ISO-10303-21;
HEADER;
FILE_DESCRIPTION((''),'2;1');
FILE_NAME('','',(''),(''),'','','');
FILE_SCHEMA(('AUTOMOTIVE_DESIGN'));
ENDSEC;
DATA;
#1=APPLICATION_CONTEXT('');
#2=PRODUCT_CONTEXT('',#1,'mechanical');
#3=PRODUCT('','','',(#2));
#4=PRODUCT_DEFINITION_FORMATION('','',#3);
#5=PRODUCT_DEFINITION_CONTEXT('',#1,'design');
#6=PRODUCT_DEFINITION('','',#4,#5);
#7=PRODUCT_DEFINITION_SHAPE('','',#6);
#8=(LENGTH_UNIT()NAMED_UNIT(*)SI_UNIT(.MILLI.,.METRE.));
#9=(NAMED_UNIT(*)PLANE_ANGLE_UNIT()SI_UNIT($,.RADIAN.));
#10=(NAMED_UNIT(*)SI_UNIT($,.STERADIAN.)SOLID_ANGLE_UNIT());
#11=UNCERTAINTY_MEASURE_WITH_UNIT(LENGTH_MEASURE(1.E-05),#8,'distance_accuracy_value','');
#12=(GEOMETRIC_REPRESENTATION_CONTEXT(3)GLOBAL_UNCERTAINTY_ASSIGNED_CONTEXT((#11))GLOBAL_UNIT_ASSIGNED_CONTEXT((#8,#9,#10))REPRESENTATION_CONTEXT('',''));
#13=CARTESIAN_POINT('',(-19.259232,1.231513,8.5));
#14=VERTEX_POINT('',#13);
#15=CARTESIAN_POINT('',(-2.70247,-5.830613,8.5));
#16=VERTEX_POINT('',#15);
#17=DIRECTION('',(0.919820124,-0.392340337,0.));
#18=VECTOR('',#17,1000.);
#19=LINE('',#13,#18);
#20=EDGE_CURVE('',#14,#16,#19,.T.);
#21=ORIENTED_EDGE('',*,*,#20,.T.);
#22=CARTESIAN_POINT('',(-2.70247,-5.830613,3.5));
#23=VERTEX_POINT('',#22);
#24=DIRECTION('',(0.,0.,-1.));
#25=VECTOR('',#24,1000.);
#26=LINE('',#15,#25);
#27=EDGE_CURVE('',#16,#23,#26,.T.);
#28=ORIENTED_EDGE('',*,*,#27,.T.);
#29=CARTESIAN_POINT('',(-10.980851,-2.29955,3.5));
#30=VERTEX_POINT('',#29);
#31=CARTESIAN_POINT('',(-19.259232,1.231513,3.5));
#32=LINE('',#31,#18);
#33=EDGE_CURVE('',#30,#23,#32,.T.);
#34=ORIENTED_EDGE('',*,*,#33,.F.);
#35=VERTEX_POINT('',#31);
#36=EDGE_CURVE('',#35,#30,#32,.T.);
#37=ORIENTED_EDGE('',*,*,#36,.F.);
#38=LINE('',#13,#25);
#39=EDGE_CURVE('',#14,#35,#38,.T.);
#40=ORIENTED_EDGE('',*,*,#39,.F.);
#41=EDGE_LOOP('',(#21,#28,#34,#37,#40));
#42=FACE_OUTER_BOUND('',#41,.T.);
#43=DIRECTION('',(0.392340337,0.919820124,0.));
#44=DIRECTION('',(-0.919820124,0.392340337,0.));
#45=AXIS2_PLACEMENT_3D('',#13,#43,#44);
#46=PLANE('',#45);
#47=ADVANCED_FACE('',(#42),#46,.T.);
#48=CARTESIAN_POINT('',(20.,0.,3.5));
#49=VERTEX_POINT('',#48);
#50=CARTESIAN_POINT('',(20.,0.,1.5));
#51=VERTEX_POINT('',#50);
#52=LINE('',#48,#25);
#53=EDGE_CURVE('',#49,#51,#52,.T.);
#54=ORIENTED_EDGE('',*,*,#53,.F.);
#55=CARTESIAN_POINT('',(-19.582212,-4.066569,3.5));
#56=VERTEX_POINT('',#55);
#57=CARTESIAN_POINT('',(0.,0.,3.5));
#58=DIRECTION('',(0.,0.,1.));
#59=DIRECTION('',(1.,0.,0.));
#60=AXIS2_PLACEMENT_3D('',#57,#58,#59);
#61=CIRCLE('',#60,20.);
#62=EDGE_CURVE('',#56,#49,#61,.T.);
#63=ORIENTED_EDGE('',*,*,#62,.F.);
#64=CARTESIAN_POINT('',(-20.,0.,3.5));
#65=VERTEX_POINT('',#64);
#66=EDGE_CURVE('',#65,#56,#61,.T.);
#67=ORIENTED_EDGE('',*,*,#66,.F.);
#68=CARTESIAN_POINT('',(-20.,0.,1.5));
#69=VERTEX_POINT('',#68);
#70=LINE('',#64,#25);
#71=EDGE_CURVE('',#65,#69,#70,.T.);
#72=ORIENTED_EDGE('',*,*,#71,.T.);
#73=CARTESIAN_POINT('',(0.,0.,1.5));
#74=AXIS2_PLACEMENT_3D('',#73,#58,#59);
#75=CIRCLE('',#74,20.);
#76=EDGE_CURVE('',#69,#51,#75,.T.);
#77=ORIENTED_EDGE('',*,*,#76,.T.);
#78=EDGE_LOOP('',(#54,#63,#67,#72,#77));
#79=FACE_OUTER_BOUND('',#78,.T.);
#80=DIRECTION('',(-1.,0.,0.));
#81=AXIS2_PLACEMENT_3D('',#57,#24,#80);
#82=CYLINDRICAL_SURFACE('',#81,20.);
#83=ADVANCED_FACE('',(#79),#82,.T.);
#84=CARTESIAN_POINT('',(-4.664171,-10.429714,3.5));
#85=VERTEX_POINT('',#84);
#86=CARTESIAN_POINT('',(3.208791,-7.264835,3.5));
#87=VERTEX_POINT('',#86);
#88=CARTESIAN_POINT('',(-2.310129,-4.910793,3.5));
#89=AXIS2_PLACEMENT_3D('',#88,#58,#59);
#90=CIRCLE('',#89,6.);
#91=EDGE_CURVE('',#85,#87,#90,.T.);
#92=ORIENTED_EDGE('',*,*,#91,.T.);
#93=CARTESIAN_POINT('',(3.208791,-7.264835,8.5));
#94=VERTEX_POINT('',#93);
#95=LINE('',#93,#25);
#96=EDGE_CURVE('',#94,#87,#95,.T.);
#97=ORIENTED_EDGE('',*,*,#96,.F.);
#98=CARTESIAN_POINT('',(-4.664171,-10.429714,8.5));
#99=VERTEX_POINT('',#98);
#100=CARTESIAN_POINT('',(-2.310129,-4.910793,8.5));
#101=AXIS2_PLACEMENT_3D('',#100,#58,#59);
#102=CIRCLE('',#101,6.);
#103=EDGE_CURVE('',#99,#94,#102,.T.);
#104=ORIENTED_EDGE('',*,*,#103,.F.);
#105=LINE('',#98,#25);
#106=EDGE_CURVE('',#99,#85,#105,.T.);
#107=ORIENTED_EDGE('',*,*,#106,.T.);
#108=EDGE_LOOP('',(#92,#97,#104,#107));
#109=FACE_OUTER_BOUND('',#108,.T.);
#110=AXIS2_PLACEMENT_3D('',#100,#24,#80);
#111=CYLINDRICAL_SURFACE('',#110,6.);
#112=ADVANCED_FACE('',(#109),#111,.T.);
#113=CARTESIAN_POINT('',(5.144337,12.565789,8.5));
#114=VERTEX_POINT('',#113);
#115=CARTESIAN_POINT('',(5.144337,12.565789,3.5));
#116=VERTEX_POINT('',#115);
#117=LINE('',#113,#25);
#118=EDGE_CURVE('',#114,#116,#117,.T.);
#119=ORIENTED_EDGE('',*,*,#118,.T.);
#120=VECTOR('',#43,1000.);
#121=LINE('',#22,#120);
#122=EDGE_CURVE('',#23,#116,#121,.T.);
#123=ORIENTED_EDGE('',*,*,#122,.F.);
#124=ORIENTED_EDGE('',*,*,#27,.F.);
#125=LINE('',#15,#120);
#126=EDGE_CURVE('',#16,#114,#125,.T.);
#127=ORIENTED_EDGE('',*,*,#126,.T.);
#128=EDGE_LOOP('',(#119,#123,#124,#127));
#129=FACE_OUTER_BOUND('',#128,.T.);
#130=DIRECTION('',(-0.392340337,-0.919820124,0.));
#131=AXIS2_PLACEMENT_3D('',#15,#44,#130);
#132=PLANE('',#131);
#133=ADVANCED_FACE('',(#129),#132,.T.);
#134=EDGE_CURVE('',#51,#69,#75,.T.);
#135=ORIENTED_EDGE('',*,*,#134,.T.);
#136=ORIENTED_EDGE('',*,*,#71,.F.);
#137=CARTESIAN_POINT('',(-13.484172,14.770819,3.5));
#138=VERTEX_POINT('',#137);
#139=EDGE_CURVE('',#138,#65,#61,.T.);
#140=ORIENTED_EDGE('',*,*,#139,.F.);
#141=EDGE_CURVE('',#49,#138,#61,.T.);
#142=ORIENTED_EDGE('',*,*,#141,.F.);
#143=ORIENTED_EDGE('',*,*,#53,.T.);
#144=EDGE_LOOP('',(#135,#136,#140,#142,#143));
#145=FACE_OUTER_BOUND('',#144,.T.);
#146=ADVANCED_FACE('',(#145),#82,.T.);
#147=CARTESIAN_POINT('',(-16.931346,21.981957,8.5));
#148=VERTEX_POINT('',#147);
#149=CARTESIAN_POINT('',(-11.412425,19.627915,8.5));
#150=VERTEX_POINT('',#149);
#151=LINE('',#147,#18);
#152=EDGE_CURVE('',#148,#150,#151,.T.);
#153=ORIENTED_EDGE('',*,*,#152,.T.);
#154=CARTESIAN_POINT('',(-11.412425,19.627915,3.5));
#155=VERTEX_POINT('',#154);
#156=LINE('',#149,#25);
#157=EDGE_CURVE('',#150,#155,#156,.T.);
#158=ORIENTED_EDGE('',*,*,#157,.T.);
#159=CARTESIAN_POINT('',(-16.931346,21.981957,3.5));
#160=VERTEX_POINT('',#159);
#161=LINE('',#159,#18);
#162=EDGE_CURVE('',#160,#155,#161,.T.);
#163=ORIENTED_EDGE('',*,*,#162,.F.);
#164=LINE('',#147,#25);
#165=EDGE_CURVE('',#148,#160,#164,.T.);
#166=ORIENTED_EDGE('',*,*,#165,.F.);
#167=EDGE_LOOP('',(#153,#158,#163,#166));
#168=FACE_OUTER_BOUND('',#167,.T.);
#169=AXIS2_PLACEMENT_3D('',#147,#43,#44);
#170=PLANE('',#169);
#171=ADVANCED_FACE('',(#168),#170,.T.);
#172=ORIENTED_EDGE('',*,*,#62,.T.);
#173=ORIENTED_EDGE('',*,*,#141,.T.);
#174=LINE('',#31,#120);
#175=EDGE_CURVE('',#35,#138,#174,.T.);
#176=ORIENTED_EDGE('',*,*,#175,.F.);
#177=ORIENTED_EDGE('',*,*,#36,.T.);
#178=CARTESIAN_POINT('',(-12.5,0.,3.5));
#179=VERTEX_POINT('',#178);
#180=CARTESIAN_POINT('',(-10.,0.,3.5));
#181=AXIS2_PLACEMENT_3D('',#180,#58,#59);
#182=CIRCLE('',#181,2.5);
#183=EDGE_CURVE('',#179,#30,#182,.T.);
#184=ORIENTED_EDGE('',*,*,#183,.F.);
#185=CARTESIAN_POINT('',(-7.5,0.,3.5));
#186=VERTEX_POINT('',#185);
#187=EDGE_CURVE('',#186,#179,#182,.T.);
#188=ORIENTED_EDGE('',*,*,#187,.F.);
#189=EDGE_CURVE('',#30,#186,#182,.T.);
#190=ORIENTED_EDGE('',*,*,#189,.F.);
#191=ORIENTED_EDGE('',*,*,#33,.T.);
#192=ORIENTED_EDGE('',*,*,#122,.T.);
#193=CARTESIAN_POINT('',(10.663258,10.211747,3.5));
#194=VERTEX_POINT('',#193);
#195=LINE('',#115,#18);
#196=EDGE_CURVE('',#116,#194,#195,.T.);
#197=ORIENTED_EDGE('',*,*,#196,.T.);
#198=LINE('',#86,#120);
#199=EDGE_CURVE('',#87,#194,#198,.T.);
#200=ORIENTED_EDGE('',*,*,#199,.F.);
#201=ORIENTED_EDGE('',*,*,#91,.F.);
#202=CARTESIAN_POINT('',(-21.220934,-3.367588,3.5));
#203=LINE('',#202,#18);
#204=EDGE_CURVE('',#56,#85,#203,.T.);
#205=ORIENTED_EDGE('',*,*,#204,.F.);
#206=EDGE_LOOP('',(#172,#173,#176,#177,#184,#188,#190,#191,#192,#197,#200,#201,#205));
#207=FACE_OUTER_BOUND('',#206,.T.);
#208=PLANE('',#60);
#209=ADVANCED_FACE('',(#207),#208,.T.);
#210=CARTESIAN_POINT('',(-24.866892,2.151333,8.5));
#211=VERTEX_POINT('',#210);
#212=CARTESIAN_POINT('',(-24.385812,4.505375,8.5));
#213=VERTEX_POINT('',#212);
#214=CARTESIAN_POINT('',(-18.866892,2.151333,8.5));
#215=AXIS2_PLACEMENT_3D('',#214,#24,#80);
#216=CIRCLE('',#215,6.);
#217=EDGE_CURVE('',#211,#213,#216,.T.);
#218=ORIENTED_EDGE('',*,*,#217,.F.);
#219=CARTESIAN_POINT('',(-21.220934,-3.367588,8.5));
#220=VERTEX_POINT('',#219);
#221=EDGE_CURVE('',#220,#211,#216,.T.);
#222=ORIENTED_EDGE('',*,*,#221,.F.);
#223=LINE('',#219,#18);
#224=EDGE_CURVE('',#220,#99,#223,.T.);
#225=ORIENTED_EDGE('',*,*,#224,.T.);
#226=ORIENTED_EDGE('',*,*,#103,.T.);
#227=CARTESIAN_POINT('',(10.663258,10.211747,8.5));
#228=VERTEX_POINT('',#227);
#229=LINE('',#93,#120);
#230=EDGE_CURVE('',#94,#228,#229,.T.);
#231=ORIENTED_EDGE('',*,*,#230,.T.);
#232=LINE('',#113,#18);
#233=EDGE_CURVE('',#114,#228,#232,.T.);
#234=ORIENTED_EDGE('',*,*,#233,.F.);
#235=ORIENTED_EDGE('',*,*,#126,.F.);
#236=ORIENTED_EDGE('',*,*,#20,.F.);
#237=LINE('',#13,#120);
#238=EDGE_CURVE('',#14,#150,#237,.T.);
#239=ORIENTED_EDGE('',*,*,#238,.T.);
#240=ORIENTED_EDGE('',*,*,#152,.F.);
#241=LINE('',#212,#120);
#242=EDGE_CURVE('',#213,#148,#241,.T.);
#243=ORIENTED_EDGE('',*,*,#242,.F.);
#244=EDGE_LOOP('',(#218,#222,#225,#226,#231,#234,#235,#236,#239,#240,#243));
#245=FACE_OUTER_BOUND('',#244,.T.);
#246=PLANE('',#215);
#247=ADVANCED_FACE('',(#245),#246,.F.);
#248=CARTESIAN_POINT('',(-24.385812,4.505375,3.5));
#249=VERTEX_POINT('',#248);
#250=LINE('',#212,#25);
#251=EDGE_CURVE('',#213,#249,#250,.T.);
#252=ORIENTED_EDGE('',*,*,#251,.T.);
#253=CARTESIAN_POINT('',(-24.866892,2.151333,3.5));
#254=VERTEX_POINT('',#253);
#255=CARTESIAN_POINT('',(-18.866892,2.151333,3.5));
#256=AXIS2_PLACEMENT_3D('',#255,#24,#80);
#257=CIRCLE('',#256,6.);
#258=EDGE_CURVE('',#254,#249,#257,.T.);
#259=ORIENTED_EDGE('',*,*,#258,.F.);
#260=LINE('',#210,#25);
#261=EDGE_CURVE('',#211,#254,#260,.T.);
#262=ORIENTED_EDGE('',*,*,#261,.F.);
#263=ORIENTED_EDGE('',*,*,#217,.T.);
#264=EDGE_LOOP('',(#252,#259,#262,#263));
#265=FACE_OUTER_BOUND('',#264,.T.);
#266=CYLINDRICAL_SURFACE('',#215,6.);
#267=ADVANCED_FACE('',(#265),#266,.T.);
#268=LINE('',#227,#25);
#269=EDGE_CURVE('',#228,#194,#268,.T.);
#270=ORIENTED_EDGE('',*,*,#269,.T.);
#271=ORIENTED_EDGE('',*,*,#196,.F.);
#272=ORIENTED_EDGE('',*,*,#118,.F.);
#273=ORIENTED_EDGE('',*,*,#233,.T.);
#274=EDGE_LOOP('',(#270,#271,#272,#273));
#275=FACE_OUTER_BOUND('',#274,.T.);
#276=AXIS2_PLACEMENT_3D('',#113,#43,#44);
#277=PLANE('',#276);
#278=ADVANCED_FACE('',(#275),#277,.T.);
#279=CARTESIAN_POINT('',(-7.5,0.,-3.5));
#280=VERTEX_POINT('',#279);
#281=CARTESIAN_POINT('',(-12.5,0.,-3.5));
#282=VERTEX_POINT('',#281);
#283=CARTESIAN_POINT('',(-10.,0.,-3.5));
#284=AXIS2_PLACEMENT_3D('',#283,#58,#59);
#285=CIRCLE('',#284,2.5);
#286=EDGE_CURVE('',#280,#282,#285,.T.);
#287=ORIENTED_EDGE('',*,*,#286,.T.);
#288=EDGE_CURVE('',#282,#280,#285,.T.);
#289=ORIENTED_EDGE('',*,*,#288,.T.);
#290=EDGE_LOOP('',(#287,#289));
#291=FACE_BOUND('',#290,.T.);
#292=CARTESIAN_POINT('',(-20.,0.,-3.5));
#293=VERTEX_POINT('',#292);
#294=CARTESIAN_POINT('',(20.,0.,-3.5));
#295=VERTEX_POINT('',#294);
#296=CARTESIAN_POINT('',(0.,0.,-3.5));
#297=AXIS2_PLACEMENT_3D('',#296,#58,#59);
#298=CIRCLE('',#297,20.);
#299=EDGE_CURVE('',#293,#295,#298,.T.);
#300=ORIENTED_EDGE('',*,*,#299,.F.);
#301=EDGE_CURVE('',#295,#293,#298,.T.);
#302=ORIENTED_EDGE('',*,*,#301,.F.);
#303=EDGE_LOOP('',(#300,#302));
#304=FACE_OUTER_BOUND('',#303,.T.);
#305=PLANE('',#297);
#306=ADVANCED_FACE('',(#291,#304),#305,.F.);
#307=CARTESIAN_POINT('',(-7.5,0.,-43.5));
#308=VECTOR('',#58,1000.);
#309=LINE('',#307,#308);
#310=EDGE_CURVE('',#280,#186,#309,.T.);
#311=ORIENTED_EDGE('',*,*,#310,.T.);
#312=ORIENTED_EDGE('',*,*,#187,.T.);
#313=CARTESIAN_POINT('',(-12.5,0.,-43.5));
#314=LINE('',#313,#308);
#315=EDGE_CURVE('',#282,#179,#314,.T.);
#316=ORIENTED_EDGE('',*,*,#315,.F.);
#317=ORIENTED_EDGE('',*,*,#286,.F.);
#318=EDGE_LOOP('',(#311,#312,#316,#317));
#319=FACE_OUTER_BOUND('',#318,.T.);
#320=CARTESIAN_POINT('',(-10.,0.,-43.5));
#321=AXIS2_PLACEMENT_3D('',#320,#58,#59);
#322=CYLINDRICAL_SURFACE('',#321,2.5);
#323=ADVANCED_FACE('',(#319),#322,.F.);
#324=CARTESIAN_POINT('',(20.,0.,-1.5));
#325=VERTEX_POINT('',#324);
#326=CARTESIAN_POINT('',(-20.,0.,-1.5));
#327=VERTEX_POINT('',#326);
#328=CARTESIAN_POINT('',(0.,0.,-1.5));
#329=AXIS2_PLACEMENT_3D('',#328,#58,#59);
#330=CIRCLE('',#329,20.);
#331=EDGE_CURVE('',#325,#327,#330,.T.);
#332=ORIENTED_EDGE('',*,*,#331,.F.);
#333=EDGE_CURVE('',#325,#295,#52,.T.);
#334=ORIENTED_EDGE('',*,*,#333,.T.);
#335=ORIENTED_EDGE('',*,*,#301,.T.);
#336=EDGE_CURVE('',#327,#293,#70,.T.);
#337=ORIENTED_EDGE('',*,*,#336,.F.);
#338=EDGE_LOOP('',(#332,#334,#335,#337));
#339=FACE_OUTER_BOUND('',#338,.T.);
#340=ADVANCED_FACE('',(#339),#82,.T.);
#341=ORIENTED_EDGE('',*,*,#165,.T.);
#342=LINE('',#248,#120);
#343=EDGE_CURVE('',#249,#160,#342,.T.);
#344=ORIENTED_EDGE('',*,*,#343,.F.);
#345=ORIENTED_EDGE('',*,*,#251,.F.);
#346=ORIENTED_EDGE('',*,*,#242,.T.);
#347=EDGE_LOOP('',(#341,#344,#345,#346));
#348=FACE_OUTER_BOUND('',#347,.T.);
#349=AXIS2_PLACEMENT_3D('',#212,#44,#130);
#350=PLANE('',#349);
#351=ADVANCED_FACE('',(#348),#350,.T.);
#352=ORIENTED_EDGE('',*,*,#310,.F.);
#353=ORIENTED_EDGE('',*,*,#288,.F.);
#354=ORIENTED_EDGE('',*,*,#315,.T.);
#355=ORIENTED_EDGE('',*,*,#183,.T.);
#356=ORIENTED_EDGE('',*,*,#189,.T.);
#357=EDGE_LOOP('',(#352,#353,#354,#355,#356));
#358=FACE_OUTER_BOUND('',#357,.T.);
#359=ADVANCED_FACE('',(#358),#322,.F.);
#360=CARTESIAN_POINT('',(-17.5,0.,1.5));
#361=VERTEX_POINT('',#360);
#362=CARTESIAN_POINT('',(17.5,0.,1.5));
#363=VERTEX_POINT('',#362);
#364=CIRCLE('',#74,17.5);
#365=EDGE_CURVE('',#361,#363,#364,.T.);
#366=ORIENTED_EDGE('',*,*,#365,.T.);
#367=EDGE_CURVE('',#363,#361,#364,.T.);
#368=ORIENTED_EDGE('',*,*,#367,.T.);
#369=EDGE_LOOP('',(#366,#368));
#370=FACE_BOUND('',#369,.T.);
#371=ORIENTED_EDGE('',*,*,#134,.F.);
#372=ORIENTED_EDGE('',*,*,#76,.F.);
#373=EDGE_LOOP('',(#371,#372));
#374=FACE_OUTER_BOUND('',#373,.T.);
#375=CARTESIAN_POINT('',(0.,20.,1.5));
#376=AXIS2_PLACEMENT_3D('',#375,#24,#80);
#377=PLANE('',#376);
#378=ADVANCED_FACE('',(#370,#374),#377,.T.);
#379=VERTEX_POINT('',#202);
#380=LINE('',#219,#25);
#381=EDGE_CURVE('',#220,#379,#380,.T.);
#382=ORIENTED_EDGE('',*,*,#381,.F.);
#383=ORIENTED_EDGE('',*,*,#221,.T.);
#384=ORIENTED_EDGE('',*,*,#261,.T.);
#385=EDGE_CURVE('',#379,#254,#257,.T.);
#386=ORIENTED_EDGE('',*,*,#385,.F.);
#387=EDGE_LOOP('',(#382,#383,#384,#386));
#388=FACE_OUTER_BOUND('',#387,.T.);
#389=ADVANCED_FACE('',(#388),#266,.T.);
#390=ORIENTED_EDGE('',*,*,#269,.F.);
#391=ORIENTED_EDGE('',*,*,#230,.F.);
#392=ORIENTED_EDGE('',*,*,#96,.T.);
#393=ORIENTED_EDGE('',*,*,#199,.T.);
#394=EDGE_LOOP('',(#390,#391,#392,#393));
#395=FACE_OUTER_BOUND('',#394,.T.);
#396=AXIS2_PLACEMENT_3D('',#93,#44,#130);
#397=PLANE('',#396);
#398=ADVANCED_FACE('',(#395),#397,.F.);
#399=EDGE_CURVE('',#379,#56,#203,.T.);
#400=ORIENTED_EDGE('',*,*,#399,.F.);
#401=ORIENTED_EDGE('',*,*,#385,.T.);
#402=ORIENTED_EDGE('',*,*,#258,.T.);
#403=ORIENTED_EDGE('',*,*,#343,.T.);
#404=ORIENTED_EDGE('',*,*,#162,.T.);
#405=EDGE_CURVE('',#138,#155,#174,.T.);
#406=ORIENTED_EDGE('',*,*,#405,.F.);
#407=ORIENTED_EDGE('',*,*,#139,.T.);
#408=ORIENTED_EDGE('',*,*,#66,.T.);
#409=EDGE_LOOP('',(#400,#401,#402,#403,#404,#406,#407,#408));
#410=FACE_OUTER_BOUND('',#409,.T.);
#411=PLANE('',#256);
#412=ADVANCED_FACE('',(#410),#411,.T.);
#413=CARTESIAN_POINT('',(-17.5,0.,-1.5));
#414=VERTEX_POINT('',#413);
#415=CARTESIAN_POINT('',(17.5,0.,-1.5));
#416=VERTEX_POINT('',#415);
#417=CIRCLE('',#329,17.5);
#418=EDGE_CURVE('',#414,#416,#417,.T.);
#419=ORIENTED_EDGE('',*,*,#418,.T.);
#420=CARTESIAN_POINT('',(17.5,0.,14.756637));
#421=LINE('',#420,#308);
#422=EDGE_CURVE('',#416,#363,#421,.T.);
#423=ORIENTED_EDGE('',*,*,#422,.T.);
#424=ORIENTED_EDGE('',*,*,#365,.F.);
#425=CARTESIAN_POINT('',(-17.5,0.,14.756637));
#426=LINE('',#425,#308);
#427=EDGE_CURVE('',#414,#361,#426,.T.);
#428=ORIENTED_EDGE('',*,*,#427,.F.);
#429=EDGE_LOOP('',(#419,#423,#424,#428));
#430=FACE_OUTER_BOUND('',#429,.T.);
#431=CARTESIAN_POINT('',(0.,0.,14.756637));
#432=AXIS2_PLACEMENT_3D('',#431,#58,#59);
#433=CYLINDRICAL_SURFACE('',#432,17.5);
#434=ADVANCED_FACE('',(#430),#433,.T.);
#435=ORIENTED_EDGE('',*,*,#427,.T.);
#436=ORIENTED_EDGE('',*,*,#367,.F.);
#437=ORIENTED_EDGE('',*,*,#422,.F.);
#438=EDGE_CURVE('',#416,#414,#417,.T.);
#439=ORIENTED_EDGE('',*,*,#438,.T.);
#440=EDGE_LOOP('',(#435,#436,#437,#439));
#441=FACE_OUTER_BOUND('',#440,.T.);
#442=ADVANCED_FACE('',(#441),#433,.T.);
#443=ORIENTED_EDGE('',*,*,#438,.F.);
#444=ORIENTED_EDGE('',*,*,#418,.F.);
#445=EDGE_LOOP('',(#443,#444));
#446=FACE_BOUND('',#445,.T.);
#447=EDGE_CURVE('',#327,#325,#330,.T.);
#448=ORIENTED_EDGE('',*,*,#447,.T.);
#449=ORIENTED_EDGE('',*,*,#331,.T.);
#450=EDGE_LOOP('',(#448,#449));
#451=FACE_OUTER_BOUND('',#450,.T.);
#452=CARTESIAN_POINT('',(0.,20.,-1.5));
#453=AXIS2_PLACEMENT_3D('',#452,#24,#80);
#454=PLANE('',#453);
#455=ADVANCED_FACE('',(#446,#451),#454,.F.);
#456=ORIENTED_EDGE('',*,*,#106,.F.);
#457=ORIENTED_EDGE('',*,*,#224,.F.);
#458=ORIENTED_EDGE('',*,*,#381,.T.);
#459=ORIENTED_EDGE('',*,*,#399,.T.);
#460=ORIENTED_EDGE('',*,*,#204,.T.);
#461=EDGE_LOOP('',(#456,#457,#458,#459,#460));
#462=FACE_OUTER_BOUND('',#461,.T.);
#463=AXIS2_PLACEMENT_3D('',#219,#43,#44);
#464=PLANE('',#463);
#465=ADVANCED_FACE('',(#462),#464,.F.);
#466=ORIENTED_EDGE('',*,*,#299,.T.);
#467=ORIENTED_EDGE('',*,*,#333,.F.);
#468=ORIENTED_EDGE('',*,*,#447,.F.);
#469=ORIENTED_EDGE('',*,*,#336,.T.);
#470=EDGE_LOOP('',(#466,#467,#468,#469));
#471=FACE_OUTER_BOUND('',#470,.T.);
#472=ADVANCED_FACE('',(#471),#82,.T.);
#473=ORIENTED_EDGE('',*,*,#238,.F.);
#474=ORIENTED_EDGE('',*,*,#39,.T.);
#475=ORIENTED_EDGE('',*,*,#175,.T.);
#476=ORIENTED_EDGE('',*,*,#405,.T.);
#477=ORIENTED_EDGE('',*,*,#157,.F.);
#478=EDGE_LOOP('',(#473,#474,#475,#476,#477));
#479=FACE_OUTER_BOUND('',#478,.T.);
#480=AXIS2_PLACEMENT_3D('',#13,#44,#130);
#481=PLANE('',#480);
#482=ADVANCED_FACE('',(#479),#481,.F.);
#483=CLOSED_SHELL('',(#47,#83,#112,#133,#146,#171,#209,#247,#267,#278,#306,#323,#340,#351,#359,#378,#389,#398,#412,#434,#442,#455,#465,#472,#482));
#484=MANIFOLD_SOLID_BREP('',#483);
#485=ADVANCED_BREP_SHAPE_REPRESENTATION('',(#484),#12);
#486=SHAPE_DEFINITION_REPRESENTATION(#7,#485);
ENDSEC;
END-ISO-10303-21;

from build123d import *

# Parameters (mm, degrees)
DISC_PROFILE_40_R      = 20
DISC_40X7_DEPTH        = 3.5
RIM_GROOVE_PROFILE_W   = 3
RIM_GROOVE_PROFILE_H   = 2.5
THROUGH_HOLE_PROFILE_R = 2.5
THROUGH_HOLE_DEPTH     = 47
U_HOOK_BOSS_DEPTH      = 5


with BuildPart() as part:
    # Disc Profile Ø40 → Disc Ø40x7 (new, symmetric)
    with BuildSketch(Plane.XY):
        Circle(DISC_PROFILE_40_R)
    extrude(amount=DISC_40X7_DEPTH, both=True)

    # Rim Groove Profile → Rim Groove (revolve, cut)
    with BuildSketch(Plane(origin=(0, 0, 0), x_dir=(0, 0, -1), z_dir=(1, 0, 0)), mode=Mode.PRIVATE) as rim_groove_sk:
        with Locations((0, 18.75)):
            Rectangle(RIM_GROOVE_PROFILE_W, RIM_GROOVE_PROFILE_H)
    revolve(rim_groove_sk.sketch.rotate(Axis((0, 0, 14.756637323), (0, 0, -1)), 90), axis=Axis((0, 0, 14.756637323), (0, 0, -1)), mode=Mode.SUBTRACT)

    # Through Hole Profile → Through Hole (cut)
    with BuildSketch(Plane.XY.offset(3.5)):
        with Locations((-10, 0)):
            Circle(THROUGH_HOLE_PROFILE_R)
    extrude(amount=-THROUGH_HOLE_DEPTH, mode=Mode.SUBTRACT)

    # U Hook Profile → U Hook Boss (add)
    with BuildSketch(Plane.XY.offset(3.5)):
        with BuildLine():
            Line((-19.259231956, 1.231512725), (-2.70246973, -5.830613343))
            Line((-2.70246973, -5.830613343), (5.144337012, 12.56578913))
            Line((5.144337012, 12.56578913), (10.663257754, 10.211747107))
            Line((10.663257754, 10.211747107), (3.208791349, -7.264835242))
            ThreePointArc((3.208791349, -7.264835242), (-0.072222189, -10.477818578), (-4.664171415, -10.429713961))
            Line((-4.664171415, -10.429713961), (-21.220933641, -3.367587893))
            ThreePointArc((-21.220933641, -3.367587893), (-24.433916977, -0.086574356), (-24.38581236, 4.505374871))
            Line((-24.38581236, 4.505374871), (-16.931345956, 21.981957221))
            Line((-16.931345956, 21.981957221), (-11.412425214, 19.627915198))
            Line((-11.412425214, 19.627915198), (-19.259231956, 1.231512725))
        make_face()
    extrude(amount=U_HOOK_BOSS_DEPTH)


solid = part.part
